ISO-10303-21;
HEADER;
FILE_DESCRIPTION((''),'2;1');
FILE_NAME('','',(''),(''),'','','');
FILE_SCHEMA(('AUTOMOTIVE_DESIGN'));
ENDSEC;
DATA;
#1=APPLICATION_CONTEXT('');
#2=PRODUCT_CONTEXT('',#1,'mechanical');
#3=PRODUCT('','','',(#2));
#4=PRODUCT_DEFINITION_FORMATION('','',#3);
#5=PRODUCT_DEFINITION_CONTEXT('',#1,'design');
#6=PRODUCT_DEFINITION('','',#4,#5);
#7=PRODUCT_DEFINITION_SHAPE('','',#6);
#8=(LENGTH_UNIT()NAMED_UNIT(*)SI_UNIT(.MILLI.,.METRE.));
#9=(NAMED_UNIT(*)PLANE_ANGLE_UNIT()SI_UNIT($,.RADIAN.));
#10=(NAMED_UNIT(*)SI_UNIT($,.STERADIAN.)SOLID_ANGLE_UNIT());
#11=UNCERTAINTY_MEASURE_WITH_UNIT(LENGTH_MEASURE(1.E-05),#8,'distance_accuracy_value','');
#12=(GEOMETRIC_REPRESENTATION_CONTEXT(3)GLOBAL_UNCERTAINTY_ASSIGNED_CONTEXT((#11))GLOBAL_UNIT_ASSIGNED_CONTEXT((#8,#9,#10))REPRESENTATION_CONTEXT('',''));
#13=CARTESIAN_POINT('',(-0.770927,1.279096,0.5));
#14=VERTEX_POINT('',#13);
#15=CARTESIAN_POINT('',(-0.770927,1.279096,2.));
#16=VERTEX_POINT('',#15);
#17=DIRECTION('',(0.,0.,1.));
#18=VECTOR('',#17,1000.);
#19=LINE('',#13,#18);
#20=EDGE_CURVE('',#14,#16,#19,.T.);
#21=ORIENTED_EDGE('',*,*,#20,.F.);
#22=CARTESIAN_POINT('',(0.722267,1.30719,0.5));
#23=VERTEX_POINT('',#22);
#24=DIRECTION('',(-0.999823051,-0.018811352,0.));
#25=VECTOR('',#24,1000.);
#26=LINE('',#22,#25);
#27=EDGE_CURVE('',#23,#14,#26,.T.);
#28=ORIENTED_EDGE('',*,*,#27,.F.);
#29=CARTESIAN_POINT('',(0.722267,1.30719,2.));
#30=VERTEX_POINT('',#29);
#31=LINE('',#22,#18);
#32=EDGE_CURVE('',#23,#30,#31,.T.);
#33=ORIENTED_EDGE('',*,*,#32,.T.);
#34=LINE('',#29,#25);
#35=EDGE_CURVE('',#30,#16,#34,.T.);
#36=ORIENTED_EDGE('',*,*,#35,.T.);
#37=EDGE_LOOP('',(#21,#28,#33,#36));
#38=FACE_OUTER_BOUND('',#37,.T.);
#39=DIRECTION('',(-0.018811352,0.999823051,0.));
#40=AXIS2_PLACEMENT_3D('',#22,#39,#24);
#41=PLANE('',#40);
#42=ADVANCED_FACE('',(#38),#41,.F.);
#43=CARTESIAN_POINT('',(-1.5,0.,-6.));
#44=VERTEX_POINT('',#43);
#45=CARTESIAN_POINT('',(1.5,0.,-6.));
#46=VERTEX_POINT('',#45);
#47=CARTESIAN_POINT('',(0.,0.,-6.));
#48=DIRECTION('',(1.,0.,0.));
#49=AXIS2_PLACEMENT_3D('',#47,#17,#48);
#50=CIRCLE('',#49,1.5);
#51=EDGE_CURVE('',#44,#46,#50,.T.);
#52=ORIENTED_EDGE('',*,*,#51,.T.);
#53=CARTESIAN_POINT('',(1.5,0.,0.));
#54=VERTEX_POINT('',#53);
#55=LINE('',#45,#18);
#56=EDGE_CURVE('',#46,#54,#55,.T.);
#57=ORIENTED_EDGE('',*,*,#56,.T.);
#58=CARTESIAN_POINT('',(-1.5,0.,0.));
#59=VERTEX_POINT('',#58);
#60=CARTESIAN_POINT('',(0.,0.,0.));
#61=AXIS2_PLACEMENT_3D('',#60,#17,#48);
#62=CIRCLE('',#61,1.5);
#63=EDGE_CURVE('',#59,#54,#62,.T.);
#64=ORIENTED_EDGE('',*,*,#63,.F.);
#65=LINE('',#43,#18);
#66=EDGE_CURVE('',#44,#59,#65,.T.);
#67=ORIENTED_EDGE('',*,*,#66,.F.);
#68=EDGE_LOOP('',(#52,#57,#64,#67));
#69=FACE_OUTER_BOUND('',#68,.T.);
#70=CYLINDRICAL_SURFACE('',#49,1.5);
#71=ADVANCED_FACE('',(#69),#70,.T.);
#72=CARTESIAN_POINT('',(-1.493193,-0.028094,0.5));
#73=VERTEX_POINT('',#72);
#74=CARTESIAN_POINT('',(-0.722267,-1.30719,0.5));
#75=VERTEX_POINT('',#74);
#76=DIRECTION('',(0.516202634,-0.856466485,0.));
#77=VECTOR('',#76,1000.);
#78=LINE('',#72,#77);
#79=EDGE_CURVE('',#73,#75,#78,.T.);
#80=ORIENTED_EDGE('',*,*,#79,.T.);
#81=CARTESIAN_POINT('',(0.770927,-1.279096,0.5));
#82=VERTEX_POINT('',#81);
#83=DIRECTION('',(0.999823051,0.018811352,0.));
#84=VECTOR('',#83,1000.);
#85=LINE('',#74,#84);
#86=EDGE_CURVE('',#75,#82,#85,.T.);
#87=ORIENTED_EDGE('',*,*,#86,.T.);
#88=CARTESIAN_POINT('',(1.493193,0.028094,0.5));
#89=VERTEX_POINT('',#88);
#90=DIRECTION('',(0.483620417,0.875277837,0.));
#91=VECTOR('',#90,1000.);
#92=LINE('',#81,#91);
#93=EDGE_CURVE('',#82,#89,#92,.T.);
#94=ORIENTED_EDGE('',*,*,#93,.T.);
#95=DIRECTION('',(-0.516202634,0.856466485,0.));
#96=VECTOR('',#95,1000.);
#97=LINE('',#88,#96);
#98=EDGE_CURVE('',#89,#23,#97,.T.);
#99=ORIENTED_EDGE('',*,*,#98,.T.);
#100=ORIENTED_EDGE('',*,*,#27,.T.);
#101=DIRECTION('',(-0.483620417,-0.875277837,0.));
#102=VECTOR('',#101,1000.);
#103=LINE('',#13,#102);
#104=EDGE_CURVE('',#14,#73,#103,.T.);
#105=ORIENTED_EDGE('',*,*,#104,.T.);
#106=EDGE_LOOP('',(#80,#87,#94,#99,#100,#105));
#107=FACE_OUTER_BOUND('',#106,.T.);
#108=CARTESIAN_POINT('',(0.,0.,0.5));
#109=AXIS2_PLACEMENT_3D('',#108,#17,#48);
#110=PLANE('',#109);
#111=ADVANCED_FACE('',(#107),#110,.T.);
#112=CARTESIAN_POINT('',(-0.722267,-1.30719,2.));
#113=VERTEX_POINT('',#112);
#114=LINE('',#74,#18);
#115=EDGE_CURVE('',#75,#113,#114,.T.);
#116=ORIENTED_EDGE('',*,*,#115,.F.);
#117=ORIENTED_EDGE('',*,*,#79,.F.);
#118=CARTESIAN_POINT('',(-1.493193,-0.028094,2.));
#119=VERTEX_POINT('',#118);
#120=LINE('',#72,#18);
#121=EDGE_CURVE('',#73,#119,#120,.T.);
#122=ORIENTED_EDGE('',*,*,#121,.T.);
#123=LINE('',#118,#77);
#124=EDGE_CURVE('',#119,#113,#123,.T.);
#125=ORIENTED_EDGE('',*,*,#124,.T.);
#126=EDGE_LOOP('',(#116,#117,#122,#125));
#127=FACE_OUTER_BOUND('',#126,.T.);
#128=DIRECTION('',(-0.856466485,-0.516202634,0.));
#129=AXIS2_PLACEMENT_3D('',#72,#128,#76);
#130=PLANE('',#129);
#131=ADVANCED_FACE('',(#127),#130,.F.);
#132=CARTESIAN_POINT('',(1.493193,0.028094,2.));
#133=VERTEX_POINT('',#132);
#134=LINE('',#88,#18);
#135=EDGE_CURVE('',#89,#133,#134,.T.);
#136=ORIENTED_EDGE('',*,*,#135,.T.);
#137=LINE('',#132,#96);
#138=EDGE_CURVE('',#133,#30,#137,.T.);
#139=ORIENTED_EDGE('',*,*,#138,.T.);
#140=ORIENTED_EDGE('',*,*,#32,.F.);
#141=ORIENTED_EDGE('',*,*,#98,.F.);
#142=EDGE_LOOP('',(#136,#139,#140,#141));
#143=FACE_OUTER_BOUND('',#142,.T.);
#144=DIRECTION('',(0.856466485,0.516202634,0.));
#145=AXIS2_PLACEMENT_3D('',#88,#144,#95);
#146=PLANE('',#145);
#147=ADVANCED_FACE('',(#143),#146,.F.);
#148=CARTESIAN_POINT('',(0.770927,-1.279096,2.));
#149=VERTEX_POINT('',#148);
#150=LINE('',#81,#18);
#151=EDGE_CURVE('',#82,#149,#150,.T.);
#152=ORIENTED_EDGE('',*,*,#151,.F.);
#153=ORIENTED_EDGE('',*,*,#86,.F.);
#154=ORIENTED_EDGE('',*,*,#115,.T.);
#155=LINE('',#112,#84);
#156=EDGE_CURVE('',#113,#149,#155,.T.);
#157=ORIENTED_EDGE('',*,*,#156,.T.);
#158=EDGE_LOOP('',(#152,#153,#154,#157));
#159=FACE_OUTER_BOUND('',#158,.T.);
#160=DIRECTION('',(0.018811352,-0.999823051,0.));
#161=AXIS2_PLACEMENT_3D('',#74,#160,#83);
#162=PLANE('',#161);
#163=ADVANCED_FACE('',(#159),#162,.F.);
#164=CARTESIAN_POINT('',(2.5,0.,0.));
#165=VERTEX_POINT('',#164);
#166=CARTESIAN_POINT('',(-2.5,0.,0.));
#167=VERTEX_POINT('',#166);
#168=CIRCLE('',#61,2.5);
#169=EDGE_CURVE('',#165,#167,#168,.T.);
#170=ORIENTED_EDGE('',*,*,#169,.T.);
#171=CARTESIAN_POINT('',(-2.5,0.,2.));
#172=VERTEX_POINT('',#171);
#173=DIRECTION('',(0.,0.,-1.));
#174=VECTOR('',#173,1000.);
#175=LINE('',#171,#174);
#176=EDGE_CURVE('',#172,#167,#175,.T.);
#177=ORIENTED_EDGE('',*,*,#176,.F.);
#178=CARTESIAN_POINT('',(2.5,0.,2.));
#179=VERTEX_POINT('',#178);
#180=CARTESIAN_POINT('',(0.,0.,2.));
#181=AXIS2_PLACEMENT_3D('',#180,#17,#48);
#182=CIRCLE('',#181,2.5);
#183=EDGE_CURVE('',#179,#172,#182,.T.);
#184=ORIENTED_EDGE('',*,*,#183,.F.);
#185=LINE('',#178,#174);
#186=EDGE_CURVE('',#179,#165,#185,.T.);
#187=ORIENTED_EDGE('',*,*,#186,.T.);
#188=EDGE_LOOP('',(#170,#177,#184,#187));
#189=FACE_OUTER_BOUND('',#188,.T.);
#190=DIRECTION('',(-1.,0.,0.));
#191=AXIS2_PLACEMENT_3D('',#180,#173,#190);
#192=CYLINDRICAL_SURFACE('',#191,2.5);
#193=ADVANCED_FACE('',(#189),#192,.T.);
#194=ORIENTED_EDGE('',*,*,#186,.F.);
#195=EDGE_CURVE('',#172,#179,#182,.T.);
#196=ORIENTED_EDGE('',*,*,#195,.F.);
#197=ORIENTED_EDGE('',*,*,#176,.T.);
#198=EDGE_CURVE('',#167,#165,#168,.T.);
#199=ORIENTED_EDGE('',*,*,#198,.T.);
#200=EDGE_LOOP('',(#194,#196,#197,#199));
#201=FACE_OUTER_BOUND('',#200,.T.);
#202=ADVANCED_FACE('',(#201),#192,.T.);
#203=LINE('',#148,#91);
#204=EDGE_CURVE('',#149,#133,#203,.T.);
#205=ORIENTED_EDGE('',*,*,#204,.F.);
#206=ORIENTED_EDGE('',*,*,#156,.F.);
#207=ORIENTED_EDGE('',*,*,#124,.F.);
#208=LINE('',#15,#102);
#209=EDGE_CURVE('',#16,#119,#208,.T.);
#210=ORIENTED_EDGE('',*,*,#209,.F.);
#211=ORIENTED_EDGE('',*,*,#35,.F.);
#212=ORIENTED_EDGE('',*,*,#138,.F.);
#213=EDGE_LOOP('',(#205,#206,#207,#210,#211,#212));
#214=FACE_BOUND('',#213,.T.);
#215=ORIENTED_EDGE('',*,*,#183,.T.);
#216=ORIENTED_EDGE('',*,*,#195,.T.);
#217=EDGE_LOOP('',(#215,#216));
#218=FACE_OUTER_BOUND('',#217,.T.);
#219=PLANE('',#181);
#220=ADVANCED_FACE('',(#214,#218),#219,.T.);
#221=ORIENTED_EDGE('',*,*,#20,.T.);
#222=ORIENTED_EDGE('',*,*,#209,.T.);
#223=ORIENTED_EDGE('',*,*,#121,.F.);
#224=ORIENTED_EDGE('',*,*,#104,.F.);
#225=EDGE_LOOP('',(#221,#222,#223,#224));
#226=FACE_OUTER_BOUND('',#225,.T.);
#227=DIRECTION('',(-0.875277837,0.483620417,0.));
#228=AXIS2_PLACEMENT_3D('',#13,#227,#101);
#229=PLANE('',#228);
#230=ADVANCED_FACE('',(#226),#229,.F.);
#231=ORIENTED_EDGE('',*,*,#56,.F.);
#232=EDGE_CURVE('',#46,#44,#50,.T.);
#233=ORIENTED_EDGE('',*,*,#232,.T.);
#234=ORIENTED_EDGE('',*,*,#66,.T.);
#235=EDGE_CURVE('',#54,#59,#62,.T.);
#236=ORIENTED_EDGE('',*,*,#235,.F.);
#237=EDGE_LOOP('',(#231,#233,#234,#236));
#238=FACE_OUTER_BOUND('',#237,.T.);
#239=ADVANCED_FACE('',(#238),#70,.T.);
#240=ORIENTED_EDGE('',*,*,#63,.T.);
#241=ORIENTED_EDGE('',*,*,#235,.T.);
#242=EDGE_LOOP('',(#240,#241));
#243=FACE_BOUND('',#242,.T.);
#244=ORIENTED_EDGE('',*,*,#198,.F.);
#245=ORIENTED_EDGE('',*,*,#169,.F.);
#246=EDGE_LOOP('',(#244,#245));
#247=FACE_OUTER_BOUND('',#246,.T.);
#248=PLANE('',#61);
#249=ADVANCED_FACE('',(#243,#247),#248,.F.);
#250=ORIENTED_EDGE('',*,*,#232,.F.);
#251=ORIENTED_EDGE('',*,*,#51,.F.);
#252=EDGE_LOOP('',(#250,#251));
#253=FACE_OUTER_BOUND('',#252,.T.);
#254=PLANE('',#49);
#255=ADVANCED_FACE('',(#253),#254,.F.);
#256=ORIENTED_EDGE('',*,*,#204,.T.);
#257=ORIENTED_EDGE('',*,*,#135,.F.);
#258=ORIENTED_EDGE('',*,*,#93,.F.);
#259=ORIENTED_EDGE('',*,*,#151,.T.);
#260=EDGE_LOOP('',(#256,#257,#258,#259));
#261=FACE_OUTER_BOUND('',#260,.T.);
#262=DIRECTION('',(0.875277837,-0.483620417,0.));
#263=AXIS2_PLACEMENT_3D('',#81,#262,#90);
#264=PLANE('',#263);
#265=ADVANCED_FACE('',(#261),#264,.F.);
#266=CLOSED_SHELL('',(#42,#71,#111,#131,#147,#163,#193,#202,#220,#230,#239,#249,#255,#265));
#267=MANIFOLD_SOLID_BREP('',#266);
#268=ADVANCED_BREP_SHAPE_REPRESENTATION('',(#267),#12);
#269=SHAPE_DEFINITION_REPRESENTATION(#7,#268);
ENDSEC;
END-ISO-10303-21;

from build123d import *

# Parameters (mm, degrees)
SKETCH1_R           = 1.5
BOSS_EXTRUDE1_DEPTH = 6
SKETCH2_R           = 2.5
BOSS_EXTRUDE2_DEPTH = 2
CUT_EXTRUDE1_DEPTH  = 1.5


with BuildPart() as part:
    # Sketch1 → Boss-Extrude1 (new body)
    with BuildSketch(Plane.XY):
        Circle(SKETCH1_R)
    extrude(amount=-BOSS_EXTRUDE1_DEPTH)

    # Sketch2 → Boss-Extrude2 (add)
    with BuildSketch(Plane.XY):
        Circle(SKETCH2_R)
    extrude(amount=BOSS_EXTRUDE2_DEPTH)

    # Sketch3 → Cut-Extrude1 (cut)
    with BuildSketch(Plane.XY.offset(2)):
        Polygon((0.722266578, 1.307190321), (-0.770926737, 1.279096365), (-1.493193314, -0.028093956), (-0.722266578, -1.307190321), (0.770926737, -1.279096365), (1.493193314, 0.028093956), align=None)
    extrude(amount=-CUT_EXTRUDE1_DEPTH, mode=Mode.SUBTRACT)


solid = part.part
